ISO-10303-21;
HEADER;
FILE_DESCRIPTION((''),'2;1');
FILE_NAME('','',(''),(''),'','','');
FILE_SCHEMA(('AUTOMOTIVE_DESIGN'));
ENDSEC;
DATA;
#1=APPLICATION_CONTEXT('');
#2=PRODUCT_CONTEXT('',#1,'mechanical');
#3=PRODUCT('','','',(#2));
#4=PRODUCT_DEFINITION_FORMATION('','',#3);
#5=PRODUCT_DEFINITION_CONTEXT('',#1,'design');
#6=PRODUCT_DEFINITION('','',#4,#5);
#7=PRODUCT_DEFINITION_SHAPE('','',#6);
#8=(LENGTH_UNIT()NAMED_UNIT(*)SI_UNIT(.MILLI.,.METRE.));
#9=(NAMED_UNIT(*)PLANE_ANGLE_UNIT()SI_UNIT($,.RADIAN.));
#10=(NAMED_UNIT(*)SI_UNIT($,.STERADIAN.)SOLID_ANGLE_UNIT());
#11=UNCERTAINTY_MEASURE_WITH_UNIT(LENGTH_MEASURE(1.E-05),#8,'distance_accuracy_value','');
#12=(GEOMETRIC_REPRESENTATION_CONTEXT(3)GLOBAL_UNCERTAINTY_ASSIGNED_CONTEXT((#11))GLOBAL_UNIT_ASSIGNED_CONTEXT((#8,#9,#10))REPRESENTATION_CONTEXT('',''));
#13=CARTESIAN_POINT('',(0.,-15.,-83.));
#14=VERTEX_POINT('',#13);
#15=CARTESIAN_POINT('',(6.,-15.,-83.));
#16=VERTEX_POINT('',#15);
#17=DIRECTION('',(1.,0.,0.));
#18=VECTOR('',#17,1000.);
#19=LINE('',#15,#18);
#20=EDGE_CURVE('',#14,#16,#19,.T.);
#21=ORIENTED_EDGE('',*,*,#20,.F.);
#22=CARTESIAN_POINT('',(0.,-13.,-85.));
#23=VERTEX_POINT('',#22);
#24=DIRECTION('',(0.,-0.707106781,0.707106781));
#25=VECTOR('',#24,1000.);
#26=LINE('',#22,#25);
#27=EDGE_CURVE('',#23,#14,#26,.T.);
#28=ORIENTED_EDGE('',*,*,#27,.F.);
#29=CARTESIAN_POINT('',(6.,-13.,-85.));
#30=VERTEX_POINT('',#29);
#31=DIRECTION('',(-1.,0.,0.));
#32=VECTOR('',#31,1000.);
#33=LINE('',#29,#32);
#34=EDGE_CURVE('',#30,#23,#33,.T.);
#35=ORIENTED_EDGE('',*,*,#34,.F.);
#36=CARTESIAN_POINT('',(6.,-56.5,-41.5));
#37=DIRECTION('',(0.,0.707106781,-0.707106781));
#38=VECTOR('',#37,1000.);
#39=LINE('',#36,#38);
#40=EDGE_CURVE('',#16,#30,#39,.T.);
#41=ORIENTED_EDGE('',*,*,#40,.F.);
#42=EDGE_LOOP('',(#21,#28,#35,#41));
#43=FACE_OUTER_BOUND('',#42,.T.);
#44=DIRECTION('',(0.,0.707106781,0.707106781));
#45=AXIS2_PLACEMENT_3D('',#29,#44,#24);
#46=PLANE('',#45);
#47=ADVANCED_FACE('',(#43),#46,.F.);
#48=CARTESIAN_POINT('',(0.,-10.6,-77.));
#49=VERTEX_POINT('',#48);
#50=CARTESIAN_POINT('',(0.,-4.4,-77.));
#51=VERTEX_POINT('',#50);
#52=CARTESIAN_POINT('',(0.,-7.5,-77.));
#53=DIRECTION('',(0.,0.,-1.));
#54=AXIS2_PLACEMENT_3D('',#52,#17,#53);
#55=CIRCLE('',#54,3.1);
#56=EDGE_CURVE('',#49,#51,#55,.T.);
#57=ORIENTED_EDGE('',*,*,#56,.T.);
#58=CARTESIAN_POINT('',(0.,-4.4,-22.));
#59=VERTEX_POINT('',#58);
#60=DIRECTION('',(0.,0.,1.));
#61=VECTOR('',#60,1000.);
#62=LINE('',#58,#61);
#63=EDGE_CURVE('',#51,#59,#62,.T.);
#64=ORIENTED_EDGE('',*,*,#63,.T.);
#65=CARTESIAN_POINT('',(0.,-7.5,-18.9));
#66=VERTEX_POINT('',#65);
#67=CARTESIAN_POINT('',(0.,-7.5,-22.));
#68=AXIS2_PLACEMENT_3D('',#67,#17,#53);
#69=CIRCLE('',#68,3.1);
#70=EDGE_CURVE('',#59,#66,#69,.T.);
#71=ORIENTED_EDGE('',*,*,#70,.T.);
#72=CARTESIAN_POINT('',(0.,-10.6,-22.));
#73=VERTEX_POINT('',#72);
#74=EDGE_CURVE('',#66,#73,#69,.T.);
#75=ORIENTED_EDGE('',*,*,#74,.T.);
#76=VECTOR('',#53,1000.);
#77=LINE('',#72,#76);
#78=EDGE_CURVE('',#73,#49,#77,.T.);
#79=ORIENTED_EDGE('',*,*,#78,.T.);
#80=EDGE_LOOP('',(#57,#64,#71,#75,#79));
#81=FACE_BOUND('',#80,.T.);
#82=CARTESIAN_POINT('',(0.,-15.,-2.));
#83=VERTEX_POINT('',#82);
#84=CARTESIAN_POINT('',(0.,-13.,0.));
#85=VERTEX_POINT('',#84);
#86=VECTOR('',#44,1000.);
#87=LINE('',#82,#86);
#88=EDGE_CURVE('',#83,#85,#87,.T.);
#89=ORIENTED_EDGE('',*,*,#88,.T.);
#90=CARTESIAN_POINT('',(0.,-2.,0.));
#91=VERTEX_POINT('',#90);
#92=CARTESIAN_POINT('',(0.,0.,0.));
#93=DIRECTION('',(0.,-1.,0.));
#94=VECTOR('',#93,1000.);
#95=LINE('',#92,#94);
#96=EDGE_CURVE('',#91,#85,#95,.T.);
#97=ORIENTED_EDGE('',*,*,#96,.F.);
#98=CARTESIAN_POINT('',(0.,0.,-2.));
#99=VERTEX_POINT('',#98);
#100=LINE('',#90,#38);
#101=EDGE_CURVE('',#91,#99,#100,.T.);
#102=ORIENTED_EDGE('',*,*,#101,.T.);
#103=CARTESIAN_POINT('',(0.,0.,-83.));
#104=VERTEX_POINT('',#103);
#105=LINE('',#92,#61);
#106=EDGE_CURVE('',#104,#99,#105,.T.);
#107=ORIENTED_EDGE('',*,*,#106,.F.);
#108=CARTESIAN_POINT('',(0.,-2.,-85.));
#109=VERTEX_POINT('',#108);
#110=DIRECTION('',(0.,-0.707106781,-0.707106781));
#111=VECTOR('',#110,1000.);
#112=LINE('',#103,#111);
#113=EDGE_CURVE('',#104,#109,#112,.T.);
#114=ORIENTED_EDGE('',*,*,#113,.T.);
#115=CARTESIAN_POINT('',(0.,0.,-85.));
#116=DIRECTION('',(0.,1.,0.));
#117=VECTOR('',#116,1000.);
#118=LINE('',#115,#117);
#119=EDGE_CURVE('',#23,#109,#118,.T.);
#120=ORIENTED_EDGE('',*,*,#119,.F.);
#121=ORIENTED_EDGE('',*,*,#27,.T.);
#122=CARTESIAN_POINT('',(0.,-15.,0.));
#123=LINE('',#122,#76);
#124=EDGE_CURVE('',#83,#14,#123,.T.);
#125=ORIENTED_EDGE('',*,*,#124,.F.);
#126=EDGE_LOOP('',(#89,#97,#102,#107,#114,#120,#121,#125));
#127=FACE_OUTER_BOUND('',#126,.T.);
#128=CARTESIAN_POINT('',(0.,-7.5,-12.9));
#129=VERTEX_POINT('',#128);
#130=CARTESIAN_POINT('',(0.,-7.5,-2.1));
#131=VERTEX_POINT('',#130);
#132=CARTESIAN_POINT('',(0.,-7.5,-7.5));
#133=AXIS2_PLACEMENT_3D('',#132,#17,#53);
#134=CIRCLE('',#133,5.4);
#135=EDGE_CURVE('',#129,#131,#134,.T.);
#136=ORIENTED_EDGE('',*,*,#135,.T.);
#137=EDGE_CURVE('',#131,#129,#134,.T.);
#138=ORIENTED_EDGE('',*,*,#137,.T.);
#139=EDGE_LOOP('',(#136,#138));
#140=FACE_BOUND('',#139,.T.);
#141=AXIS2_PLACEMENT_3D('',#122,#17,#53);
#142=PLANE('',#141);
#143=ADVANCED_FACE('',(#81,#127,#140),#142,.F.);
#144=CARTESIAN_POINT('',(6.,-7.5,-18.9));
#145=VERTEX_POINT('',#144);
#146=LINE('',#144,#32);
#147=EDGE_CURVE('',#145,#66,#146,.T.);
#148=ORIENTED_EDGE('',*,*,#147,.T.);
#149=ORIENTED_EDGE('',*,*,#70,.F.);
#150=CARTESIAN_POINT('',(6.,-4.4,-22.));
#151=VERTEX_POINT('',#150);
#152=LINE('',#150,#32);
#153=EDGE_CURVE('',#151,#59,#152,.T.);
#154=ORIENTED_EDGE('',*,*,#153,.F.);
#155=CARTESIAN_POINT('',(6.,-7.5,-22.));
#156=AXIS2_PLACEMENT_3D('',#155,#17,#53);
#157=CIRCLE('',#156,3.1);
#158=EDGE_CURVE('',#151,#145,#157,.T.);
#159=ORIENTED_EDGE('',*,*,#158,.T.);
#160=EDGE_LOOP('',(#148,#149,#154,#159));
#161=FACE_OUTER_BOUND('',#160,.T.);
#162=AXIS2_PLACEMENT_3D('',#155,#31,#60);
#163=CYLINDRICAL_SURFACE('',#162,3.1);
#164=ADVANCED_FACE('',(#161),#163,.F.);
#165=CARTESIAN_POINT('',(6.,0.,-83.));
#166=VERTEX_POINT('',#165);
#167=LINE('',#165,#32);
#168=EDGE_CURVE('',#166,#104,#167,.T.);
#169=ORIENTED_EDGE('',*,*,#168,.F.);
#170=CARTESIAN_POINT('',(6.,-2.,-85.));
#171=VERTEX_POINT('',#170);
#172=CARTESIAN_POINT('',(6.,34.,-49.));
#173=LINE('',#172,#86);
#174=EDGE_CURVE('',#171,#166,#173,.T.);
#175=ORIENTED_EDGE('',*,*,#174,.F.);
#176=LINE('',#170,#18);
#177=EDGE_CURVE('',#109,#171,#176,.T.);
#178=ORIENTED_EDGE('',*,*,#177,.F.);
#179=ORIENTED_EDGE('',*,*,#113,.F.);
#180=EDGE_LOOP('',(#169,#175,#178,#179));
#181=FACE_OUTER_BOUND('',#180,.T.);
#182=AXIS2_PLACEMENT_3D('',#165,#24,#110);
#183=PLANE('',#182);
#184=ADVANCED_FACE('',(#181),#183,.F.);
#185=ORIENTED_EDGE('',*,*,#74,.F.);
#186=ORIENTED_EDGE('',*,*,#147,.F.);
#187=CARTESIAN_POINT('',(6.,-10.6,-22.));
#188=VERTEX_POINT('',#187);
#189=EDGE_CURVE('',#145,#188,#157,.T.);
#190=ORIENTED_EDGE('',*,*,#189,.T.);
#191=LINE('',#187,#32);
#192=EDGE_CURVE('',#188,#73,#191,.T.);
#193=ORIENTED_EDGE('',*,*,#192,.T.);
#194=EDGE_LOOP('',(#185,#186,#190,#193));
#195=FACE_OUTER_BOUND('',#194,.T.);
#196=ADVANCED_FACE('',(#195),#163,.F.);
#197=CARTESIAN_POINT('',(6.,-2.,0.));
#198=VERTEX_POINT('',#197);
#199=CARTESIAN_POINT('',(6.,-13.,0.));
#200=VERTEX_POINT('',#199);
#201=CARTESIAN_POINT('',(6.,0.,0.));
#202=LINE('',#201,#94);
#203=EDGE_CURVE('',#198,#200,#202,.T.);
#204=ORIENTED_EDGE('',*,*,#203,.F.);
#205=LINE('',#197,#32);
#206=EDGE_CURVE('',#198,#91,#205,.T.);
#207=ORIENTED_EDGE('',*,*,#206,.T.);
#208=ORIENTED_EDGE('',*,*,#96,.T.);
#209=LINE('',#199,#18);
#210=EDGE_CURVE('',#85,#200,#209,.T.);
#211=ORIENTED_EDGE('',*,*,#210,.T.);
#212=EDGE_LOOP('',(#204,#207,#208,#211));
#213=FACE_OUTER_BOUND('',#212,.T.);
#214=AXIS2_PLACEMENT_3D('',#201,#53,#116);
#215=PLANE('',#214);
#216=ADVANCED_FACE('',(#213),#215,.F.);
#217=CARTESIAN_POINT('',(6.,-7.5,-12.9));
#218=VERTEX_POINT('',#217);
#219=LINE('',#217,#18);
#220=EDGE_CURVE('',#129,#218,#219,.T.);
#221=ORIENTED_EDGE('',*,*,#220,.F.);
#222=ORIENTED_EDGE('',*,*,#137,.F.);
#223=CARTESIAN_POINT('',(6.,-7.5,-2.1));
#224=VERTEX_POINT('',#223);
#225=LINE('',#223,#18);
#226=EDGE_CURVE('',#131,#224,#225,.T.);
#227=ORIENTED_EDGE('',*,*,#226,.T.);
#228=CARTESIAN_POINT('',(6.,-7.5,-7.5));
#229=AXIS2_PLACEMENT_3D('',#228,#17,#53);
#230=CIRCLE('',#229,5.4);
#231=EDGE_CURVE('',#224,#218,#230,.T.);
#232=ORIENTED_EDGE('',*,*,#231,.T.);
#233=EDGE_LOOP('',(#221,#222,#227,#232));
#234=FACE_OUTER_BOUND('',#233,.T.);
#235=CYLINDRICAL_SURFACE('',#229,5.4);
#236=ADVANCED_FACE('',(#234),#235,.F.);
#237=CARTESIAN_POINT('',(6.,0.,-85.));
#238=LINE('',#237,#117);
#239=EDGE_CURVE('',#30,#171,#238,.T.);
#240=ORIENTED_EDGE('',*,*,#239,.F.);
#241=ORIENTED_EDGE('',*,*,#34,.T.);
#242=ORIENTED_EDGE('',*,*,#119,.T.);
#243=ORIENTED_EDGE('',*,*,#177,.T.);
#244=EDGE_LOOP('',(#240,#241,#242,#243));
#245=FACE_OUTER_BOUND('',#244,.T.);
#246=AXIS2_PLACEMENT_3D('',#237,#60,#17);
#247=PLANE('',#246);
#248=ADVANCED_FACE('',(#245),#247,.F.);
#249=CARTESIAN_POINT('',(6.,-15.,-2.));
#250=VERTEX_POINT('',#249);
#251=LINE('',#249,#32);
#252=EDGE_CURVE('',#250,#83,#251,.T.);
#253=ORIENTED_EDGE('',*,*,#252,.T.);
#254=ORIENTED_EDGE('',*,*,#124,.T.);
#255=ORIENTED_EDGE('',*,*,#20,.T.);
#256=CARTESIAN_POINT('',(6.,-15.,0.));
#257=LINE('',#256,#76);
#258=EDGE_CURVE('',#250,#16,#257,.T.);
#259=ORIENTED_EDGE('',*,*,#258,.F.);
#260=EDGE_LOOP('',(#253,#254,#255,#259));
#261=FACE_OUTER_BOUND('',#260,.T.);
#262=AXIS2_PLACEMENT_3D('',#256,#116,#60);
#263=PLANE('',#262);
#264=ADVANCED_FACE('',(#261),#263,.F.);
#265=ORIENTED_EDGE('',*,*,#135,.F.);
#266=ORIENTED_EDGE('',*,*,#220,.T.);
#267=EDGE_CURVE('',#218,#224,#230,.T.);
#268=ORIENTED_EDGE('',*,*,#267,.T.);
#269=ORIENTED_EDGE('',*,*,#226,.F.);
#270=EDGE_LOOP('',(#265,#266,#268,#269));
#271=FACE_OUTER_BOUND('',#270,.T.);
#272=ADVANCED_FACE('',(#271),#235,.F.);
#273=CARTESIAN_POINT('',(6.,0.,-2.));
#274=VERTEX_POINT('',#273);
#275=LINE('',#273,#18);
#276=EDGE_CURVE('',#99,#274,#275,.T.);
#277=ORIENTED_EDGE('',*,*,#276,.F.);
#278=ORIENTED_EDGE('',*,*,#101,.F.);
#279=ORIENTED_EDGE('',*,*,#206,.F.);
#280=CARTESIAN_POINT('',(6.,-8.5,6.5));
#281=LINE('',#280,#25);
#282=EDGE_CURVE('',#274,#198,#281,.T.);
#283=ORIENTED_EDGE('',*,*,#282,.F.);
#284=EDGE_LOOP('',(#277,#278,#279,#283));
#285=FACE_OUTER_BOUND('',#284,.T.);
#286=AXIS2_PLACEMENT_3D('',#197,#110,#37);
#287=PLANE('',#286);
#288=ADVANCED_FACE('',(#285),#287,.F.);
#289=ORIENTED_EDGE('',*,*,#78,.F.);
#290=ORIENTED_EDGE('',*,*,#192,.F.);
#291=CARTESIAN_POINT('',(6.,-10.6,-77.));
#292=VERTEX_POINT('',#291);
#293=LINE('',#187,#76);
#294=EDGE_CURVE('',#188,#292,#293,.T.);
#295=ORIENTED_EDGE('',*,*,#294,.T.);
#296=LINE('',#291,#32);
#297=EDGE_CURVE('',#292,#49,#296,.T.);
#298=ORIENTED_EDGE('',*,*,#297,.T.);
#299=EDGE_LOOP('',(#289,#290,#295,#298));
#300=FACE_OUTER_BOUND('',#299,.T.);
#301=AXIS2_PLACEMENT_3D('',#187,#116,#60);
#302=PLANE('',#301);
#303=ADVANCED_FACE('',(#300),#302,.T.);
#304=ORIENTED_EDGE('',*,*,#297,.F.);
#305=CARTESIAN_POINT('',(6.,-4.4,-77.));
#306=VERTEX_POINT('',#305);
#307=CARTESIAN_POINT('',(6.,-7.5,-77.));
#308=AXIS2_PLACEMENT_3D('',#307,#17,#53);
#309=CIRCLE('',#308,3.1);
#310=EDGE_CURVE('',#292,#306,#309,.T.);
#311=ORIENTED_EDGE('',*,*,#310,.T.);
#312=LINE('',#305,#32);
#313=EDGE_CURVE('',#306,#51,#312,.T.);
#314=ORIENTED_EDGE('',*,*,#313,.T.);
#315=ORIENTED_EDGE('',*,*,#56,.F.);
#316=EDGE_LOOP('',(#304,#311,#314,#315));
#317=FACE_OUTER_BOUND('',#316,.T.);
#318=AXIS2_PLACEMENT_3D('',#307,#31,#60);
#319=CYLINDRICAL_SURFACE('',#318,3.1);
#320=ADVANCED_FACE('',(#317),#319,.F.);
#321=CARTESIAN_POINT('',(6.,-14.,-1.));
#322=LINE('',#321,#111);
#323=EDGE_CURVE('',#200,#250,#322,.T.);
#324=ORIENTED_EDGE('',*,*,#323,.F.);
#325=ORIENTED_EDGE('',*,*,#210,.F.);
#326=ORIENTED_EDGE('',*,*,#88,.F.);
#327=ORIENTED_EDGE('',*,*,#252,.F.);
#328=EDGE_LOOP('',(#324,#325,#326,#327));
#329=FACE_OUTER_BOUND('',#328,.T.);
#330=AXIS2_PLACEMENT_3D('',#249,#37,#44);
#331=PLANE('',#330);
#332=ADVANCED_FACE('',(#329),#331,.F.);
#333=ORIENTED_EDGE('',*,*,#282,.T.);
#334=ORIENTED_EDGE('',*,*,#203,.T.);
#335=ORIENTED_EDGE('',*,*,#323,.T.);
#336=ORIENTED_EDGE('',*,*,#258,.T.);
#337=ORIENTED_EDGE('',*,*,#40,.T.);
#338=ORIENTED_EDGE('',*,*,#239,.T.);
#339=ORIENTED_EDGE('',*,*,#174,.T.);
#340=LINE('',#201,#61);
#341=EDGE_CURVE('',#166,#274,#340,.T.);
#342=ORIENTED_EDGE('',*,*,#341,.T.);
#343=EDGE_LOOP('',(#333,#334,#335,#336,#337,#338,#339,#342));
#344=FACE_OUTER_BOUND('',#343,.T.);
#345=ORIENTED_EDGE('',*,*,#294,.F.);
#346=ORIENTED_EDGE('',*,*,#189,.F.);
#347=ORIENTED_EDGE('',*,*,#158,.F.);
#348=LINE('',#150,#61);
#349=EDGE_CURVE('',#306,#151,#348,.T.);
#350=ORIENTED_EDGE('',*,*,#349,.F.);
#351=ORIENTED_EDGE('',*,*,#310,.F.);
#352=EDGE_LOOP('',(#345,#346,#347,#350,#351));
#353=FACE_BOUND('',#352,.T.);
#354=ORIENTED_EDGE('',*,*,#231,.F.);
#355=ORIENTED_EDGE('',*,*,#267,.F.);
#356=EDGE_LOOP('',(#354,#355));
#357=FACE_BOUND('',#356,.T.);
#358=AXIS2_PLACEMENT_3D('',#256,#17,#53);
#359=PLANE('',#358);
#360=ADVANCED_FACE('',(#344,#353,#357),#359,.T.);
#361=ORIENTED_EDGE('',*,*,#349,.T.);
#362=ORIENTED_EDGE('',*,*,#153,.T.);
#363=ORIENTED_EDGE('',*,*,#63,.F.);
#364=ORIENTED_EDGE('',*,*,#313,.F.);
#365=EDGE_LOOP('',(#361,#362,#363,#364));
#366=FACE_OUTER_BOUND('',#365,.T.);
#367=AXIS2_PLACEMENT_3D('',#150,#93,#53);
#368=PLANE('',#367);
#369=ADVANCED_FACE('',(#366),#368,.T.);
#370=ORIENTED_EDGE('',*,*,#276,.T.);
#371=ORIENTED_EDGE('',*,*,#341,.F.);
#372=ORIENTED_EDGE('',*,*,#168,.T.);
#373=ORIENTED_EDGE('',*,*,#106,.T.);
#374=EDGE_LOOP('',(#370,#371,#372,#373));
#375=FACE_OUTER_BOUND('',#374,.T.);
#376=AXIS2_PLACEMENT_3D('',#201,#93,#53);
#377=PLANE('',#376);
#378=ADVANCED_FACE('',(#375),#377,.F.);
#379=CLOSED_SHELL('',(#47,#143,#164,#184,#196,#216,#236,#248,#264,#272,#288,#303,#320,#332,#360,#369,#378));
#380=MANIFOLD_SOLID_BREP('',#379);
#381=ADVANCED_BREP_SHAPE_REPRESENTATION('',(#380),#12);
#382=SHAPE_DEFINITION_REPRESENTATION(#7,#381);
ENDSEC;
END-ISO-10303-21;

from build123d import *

# Parameters (mm, degrees)
SKETCH1_W              = 85
SKETCH1_H              = 15
EXTRUDE1_DEPTH         = 6
M12X1_0_TAPPED_HOLE1_D = 10.8
CHAMFER1_SIZE          = 2


with BuildPart() as part:
    # Sketch1 → Extrude1 (new body)
    with BuildSketch(Plane(origin=(0, 0, 0), x_dir=(0, 0, -1), z_dir=(1, 0, 0))):
        with Locations((42.5, -7.5)):
            Rectangle(SKETCH1_W, SKETCH1_H)
        with BuildLine():
            Line((22, -4.4), (77, -4.4))
            ThreePointArc((77, -4.4), (80.1, -7.5), (77, -10.6))
            Line((77, -10.6), (22, -10.6))
            ThreePointArc((22, -10.6), (18.9, -7.5), (22, -4.4))
        make_face(mode=Mode.SUBTRACT)
    extrude(amount=EXTRUDE1_DEPTH)

    # M12x1.0 Tapped Hole1 (through all)
    with Locations(Plane(origin=(6, 0, 0), x_dir=(0, 0, -1), z_dir=(1, 0, 0))):
        with Locations((7.5, -7.5)):
            Hole(M12X1_0_TAPPED_HOLE1_D / 2)

    # Chamfer1
    chamfer1_edges = [part.edges().sort_by_distance(p)[0] for p in [
        (3, 0, 0),
        (3, 0, -85),
        (3, -15, -85),
        (3, -15, 0),
    ]]
    chamfer(chamfer1_edges, length=CHAMFER1_SIZE)


solid = part.part
